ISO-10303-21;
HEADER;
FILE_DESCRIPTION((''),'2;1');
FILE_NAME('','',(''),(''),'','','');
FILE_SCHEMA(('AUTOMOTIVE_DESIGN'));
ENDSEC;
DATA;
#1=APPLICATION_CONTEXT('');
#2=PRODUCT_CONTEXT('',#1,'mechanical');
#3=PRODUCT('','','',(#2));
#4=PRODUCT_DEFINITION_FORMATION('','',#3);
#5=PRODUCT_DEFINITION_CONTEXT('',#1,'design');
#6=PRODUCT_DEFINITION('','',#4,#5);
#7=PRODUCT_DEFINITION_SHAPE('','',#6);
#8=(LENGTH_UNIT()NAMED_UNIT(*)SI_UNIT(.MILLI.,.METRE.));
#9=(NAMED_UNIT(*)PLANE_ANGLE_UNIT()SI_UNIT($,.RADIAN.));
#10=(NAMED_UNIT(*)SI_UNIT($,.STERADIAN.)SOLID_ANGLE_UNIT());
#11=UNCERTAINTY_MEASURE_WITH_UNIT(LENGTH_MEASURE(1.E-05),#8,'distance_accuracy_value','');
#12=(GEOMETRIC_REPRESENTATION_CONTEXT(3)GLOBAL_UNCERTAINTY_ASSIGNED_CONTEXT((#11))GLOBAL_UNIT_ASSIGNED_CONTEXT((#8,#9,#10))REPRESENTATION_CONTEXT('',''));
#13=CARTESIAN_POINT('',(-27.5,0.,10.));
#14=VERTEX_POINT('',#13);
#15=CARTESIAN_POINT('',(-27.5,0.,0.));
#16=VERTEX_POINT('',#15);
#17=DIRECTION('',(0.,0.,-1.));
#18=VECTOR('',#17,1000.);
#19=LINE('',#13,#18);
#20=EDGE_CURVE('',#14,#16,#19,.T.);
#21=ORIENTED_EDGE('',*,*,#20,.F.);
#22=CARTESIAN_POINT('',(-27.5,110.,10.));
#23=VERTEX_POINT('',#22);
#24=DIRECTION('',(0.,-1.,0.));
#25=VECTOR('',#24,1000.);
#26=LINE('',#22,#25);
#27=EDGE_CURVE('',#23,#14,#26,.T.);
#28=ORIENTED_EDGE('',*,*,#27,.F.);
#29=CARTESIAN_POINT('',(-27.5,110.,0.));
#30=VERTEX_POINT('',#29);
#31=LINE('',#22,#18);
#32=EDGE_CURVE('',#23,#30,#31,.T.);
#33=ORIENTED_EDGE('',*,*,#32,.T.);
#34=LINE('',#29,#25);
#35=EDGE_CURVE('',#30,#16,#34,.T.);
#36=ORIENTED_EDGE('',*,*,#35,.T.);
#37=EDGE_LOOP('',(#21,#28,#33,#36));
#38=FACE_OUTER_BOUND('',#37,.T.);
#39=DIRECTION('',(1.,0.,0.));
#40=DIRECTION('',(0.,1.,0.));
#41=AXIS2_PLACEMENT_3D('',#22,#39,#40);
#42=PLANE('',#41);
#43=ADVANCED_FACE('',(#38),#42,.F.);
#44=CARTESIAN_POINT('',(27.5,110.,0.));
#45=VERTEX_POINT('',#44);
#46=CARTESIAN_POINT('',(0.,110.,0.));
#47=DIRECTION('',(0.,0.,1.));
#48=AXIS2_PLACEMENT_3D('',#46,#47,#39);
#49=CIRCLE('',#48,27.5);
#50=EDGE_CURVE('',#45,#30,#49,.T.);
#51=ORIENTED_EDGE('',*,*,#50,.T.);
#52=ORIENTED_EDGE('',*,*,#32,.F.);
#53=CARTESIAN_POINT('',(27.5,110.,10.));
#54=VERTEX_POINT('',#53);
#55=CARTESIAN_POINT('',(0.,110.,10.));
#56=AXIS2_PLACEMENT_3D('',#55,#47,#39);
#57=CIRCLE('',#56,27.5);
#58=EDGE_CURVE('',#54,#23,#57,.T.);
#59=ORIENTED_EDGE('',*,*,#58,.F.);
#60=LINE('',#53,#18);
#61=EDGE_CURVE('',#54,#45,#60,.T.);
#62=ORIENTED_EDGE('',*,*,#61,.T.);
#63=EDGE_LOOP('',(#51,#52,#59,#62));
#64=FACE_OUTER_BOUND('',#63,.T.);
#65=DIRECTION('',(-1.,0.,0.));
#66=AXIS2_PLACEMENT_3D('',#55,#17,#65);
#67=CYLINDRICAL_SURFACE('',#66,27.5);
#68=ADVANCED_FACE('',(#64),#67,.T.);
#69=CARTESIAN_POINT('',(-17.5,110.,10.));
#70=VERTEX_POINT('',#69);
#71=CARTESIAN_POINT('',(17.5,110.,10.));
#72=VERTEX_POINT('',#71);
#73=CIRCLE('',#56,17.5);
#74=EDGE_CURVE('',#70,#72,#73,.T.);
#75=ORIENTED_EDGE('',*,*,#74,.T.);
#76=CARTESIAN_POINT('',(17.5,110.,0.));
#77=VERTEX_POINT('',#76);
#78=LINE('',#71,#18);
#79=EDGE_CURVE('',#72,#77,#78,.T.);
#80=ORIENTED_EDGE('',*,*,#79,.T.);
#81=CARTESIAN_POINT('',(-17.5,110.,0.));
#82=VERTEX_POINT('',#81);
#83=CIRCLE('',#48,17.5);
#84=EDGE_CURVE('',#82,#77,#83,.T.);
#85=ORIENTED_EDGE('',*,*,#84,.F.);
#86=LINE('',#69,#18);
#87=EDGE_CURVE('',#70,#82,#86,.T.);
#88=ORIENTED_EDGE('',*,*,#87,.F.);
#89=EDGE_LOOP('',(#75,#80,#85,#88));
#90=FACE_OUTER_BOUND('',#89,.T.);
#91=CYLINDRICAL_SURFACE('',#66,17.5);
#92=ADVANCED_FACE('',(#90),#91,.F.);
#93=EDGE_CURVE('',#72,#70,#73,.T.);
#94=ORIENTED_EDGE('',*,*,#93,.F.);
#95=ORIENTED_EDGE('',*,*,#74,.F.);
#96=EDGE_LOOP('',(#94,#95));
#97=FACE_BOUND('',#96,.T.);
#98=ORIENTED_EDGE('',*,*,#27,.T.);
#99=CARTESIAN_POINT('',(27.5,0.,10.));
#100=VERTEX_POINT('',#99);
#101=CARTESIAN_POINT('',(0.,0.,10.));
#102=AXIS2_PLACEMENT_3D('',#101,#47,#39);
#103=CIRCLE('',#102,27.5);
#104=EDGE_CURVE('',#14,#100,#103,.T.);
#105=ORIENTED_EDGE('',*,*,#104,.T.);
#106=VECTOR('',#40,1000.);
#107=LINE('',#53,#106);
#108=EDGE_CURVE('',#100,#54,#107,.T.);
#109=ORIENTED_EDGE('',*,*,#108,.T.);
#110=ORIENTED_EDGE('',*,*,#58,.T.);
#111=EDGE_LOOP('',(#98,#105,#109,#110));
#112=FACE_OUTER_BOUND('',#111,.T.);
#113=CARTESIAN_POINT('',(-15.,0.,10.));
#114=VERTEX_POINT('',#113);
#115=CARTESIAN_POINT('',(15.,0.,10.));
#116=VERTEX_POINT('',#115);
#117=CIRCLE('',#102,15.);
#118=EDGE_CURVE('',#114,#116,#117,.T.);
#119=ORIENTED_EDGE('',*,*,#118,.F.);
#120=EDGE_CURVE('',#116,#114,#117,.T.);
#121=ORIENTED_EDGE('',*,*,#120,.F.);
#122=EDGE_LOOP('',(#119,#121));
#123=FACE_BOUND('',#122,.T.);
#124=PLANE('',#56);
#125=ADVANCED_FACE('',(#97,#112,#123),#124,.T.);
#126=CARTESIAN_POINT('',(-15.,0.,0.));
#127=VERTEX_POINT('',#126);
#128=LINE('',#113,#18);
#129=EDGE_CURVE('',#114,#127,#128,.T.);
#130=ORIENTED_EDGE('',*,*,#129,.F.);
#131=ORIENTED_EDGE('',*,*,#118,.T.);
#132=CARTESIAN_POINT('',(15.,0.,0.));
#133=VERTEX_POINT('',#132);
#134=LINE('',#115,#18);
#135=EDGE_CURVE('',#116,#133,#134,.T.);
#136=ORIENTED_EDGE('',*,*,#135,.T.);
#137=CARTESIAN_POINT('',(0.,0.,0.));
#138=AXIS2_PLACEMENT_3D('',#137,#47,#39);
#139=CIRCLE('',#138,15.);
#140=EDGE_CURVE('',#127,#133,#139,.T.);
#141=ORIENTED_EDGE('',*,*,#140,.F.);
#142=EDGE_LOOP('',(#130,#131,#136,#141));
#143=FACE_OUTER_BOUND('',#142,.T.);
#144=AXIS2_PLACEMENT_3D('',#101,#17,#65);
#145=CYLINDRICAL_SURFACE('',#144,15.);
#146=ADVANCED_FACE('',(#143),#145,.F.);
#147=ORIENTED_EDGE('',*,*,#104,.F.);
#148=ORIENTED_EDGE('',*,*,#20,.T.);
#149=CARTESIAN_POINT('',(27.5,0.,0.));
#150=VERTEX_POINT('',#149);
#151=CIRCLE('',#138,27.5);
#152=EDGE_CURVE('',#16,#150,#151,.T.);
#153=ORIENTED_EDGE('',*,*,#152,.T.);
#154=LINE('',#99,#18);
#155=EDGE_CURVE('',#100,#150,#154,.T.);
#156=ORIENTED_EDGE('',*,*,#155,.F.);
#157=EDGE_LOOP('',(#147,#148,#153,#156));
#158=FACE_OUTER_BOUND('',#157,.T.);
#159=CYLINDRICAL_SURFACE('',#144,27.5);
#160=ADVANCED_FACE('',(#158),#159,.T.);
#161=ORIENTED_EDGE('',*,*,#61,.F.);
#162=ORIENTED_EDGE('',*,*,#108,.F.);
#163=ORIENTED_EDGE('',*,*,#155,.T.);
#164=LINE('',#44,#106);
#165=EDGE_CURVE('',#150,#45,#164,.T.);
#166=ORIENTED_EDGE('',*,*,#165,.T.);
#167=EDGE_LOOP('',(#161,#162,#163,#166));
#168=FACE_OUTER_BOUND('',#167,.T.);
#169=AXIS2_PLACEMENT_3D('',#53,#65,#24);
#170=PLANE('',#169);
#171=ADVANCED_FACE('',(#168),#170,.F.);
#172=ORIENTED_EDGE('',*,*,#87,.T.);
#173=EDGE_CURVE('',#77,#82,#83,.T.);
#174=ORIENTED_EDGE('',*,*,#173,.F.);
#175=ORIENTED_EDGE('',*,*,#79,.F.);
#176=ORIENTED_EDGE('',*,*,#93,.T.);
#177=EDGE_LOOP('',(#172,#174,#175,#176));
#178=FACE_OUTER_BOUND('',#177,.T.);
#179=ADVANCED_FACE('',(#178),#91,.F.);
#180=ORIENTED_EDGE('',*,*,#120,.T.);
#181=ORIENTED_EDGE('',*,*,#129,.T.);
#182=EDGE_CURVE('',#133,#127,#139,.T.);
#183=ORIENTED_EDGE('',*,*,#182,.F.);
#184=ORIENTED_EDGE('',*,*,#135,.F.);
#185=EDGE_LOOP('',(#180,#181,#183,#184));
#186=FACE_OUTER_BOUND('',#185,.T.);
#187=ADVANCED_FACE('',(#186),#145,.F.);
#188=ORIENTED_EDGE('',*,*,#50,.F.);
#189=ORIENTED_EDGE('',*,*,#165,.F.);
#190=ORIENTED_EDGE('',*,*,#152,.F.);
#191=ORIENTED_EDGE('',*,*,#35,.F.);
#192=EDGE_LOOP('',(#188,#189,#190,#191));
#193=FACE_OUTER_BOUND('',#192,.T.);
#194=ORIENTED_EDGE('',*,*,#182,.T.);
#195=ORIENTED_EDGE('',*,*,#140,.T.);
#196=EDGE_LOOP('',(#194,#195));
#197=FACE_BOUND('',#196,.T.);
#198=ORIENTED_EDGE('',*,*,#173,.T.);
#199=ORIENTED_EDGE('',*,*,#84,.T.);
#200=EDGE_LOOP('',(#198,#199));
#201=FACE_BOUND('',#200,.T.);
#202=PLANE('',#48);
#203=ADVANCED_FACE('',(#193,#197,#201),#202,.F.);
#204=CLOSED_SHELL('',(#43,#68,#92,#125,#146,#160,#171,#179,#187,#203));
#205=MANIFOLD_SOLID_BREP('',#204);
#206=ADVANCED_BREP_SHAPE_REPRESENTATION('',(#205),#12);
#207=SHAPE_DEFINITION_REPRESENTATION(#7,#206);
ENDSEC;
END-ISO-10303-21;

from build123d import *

# Parameters (mm, degrees)
SKETCH1_R           = 15
SKETCH1_R_2         = 17.5
BOSS_EXTRUDE1_DEPTH = 10


with BuildPart() as part:
    # Sketch1 → Boss-Extrude1 (new body)
    with BuildSketch(Plane.XY):
        with BuildLine():
            Line((-27.5, 110), (-27.5, 0))
            ThreePointArc((-27.5, 0), (0, -27.5), (27.5, 0))
            Line((27.5, 0), (27.5, 110))
            ThreePointArc((27.5, 110), (0, 137.5), (-27.5, 110))
        make_face()
        Circle(SKETCH1_R, mode=Mode.SUBTRACT)
        with Locations((0, 110)):
            Circle(SKETCH1_R_2, mode=Mode.SUBTRACT)
    extrude(amount=BOSS_EXTRUDE1_DEPTH)


solid = part.part
